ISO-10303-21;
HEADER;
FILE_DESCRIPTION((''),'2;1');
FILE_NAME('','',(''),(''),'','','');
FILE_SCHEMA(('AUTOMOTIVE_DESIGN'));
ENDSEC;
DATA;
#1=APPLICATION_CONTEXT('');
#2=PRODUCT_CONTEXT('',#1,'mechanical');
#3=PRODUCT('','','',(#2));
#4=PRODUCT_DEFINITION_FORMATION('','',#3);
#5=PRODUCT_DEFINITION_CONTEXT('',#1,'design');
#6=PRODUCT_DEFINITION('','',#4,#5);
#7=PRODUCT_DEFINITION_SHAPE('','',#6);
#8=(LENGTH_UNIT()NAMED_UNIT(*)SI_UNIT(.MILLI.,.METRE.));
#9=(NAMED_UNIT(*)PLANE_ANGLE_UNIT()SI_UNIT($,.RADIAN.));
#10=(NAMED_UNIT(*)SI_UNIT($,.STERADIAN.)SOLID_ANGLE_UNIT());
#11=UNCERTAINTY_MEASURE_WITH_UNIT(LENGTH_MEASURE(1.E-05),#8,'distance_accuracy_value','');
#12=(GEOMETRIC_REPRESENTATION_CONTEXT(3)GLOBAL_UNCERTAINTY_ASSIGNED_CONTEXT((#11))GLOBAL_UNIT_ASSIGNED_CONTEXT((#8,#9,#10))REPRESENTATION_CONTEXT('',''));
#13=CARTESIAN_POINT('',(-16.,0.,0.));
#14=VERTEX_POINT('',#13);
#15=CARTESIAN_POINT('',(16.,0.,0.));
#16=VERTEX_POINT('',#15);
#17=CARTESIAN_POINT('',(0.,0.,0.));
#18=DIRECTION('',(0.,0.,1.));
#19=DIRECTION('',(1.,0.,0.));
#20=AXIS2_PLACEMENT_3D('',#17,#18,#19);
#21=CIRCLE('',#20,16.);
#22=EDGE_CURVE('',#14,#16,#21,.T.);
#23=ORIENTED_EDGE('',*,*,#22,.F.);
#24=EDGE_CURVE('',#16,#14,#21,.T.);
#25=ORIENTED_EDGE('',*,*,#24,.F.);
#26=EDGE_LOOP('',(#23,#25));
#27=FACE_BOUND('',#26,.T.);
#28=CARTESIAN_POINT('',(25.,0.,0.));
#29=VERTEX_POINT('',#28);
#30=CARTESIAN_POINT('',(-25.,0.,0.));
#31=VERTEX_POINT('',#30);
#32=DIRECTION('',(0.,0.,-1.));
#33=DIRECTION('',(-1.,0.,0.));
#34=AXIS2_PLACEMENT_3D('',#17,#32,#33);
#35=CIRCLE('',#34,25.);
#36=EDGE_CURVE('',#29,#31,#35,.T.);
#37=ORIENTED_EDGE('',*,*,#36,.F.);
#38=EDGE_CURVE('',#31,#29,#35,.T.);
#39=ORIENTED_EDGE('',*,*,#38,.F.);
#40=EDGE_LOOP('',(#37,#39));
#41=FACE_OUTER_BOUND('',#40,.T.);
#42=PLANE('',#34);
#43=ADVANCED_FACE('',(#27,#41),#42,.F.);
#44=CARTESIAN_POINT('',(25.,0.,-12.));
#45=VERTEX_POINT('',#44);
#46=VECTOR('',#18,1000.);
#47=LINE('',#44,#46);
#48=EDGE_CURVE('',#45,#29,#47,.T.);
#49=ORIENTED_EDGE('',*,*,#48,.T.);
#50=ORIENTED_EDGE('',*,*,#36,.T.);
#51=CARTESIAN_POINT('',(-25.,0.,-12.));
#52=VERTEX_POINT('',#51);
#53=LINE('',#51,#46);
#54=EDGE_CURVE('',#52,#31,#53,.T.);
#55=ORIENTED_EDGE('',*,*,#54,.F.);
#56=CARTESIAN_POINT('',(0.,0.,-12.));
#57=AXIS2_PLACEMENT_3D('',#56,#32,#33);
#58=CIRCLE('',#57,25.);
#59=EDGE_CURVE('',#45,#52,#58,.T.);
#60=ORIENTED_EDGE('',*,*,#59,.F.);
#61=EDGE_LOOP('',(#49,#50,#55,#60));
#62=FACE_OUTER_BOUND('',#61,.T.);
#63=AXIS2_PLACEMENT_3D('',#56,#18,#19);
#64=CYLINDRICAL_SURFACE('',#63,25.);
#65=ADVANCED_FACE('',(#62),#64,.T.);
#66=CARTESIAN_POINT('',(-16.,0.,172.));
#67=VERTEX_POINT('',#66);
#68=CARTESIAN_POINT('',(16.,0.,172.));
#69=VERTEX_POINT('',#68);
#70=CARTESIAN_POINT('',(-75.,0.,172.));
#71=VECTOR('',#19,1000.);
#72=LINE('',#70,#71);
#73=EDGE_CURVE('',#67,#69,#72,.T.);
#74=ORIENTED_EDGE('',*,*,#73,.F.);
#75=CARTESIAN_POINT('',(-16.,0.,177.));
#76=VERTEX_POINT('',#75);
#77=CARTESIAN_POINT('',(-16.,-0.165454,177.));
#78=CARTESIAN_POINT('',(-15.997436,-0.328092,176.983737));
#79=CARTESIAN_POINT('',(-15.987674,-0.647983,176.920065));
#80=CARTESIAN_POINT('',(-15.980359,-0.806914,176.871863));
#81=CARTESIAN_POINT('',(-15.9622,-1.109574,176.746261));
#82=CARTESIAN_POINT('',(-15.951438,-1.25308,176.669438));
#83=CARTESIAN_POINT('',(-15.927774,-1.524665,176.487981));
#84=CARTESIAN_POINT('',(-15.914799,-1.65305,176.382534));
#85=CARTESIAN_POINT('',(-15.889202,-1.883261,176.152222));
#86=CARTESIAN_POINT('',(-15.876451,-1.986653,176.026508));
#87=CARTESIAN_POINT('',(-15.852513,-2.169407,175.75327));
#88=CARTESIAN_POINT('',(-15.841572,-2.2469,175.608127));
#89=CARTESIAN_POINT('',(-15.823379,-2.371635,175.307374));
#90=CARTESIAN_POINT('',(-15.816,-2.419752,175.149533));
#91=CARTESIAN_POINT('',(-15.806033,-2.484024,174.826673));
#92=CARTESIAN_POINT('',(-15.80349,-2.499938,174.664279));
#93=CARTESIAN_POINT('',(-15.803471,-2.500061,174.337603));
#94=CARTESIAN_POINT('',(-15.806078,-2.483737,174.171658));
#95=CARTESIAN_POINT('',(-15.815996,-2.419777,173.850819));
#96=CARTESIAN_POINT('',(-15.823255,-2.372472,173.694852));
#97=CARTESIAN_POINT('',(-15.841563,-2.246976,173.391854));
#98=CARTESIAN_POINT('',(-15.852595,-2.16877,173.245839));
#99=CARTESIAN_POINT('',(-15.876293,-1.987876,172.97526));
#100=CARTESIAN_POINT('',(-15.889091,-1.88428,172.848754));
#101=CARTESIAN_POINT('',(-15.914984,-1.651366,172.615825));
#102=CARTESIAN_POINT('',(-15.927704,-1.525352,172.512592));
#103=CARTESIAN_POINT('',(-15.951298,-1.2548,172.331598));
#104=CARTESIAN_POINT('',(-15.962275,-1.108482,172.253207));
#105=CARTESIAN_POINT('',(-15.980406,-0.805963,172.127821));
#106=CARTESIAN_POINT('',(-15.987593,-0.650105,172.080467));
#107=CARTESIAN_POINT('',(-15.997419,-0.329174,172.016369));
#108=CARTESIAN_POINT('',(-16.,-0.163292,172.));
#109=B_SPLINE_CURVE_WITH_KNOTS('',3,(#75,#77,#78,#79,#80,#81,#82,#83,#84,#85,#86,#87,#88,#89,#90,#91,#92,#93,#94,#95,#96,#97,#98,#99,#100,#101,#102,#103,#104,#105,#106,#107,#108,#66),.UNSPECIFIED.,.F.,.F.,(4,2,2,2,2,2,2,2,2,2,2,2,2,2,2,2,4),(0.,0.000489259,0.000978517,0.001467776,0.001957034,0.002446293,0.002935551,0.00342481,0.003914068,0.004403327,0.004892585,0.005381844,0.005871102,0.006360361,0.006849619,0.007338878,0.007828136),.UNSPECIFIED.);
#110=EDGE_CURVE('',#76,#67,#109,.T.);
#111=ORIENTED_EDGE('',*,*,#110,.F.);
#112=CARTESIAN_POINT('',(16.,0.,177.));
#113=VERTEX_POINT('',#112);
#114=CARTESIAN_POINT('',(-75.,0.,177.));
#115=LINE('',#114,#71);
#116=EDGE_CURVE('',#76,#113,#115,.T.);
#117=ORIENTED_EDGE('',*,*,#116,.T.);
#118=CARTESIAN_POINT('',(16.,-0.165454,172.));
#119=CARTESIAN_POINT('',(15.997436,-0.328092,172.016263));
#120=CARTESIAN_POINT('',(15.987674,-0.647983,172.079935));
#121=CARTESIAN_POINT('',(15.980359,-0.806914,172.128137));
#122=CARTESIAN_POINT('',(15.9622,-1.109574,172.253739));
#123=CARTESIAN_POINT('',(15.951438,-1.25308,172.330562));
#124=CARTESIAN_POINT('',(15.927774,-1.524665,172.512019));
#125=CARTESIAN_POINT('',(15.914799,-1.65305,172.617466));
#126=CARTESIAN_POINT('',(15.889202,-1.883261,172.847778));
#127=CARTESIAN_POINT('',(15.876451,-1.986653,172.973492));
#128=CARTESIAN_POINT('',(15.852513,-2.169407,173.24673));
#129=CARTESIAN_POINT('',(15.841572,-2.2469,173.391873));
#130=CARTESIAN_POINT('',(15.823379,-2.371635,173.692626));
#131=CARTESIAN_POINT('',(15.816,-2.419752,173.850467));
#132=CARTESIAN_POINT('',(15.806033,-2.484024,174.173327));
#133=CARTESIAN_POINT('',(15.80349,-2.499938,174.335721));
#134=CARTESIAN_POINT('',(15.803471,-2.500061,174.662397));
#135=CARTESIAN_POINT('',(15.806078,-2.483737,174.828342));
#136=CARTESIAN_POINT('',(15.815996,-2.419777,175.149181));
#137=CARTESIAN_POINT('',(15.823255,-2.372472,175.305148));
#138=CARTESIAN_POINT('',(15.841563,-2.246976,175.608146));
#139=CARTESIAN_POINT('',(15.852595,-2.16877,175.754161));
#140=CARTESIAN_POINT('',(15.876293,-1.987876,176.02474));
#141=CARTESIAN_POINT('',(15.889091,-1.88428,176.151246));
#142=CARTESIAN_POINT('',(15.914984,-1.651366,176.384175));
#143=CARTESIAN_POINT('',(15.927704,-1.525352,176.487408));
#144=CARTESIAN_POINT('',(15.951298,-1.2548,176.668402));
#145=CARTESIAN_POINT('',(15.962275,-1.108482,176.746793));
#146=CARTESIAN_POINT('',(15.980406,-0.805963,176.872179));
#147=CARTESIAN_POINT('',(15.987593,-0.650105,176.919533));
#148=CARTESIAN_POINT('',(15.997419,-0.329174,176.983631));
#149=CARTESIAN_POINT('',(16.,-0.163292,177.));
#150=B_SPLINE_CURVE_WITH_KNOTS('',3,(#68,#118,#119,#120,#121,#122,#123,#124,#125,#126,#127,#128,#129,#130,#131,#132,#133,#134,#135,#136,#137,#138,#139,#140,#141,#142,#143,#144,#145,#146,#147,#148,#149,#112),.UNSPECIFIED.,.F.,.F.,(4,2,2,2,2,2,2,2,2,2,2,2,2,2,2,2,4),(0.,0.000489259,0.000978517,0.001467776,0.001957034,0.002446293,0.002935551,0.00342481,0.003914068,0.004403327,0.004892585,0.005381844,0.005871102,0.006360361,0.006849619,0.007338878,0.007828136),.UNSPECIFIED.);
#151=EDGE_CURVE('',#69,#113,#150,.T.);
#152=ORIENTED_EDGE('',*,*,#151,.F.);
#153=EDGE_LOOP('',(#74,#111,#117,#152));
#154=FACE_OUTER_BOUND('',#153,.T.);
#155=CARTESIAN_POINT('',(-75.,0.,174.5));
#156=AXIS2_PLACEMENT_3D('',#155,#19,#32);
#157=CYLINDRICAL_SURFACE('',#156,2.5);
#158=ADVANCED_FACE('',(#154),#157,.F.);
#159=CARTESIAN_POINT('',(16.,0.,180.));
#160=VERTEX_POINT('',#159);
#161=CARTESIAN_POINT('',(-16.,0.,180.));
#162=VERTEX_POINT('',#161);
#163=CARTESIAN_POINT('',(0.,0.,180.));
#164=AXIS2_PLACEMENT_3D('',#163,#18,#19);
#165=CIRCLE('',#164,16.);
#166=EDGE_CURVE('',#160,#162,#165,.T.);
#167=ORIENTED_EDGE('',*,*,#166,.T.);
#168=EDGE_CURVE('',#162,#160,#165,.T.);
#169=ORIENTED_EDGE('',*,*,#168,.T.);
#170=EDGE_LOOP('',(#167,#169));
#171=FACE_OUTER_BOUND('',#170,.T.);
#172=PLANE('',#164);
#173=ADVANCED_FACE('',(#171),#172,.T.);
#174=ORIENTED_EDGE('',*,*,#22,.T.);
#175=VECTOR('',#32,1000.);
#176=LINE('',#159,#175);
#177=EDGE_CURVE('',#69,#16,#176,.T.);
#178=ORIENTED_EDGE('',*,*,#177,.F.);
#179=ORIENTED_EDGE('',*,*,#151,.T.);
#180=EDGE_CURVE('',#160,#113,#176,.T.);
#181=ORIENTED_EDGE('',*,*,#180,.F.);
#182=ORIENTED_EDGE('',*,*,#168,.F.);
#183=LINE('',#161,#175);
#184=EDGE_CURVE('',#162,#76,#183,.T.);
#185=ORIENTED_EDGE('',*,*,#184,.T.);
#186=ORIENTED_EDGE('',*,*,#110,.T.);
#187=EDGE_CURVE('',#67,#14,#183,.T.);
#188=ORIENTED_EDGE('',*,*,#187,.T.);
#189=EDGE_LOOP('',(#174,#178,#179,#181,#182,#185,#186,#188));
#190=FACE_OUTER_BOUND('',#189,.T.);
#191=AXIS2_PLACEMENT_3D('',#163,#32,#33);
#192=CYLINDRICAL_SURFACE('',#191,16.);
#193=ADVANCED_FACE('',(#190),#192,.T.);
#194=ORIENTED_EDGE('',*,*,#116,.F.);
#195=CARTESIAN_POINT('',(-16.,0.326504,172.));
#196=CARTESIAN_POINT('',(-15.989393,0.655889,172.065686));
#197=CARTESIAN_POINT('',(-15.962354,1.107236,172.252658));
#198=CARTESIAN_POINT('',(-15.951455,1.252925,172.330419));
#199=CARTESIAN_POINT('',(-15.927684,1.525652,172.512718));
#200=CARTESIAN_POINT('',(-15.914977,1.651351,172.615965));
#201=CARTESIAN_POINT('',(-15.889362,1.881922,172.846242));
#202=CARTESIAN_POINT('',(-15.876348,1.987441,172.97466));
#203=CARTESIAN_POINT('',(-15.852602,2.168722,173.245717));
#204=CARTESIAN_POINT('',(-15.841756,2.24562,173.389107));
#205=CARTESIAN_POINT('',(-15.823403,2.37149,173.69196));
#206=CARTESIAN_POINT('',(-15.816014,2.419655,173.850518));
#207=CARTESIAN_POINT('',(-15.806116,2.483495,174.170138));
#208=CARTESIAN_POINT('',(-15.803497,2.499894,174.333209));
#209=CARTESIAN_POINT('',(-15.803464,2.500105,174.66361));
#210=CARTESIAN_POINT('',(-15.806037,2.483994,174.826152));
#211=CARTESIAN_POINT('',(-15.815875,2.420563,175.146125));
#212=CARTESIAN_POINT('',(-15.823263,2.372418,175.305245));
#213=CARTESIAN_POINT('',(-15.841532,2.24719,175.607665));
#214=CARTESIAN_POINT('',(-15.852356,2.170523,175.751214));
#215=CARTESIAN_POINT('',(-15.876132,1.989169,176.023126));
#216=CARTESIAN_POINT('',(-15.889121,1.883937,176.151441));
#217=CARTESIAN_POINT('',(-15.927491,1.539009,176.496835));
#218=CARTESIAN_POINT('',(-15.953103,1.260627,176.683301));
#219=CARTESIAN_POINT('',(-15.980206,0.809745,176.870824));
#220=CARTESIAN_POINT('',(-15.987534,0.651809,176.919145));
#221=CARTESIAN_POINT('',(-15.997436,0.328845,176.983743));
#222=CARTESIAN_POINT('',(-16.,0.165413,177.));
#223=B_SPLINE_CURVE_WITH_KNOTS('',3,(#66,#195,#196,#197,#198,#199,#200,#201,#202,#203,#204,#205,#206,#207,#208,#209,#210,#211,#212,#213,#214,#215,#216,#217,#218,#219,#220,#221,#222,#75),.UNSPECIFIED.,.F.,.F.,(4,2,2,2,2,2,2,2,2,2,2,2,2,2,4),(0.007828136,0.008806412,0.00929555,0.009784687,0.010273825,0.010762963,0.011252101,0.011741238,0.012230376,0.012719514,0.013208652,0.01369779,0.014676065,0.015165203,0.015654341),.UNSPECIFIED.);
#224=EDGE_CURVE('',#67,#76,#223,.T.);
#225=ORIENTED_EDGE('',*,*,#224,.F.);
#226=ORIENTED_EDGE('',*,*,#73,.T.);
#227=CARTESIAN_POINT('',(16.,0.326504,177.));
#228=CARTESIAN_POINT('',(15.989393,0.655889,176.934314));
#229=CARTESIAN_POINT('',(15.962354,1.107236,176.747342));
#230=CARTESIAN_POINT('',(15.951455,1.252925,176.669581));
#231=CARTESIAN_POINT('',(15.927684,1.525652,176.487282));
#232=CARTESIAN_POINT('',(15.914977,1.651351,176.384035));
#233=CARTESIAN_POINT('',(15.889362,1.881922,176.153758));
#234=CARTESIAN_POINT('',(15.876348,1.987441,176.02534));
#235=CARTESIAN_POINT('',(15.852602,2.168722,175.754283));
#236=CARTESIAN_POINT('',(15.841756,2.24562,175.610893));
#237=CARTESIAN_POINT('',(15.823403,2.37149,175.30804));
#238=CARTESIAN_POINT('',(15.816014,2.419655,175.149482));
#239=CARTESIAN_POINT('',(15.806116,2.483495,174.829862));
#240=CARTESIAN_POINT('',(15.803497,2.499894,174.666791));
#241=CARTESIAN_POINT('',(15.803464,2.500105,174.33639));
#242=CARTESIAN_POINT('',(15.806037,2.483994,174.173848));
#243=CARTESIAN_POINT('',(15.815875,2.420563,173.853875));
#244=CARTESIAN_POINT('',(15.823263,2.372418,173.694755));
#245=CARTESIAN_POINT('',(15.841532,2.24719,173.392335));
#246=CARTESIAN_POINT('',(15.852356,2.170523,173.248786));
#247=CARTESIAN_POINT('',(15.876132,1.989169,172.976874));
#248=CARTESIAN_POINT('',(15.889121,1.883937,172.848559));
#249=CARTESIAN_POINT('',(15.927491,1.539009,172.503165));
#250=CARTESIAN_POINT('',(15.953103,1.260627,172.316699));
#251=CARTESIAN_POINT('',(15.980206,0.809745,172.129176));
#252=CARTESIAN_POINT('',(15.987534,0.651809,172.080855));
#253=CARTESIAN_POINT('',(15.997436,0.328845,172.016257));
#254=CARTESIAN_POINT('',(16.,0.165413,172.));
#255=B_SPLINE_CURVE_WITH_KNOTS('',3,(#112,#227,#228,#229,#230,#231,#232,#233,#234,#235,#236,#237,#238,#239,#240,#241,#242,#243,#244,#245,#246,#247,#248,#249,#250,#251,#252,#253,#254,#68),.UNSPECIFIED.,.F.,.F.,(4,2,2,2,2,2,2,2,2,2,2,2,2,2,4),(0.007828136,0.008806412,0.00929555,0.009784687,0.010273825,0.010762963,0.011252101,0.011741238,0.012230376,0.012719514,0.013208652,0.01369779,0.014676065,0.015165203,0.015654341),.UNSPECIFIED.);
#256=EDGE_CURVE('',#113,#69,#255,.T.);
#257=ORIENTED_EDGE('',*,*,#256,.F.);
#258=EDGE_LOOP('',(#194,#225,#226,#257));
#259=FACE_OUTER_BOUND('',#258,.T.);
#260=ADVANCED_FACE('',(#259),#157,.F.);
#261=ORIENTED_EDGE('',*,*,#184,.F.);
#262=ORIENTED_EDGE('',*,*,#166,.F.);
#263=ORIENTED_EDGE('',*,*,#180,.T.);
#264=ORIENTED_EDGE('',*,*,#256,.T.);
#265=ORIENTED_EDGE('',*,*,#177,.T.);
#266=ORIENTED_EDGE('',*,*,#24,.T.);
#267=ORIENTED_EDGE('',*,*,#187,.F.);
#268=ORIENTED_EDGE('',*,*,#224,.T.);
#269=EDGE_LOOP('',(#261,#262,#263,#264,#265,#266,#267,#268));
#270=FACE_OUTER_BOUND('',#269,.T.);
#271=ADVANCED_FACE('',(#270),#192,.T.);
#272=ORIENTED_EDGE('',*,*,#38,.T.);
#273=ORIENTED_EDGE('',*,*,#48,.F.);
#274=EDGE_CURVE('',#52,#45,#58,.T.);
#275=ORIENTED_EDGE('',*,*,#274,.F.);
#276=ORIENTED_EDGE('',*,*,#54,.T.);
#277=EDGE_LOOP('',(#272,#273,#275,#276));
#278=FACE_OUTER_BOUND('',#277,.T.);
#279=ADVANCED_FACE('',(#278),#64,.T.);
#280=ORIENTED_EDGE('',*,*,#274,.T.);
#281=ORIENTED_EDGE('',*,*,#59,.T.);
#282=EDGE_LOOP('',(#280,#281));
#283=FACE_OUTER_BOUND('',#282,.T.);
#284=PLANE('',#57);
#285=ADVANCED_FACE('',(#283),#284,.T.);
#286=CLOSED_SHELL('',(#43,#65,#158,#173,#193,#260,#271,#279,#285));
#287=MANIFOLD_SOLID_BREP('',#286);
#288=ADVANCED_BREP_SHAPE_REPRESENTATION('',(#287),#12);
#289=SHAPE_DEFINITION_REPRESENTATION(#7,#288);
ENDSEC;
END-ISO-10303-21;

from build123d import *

# Parameters (mm, degrees)
SHANK_PROFILE_32_R     = 16
SHANK_32X180_DEPTH     = 180
HEAD_PROFILE_50_R      = 25
HEAD_50X12_DEPTH       = 12
CROSS_HOLE_PROFILE_5_R = 2.5
CROSS_HOLE_5_DEPTH     = 75


with BuildPart() as part:
    # Shank Profile Ø32 → Shank Ø32x180 (new body)
    with BuildSketch(Plane.XY):
        with Locations(Location((0, 0, 0), (0, 0, 180))):
            Circle(SHANK_PROFILE_32_R)
    extrude(amount=SHANK_32X180_DEPTH)

    # Head Profile Ø50 → Head Ø50x12 (add)
    with BuildSketch(Plane(origin=(0, 0, 0), x_dir=(-1, 0, 0), z_dir=(0, 0, -1))):
        Circle(HEAD_PROFILE_50_R)
    extrude(amount=HEAD_50X12_DEPTH)

    # Cross Hole Profile Ø5 → Cross Hole Ø5 (cut, symmetric)
    with BuildSketch(Plane(origin=(0, 0, 0), x_dir=(0, 0, -1), z_dir=(1, 0, 0))):
        with Locations(Location((-174.5, 0, 0), (0, 0, 180))):
            Circle(CROSS_HOLE_PROFILE_5_R)
    extrude(amount=CROSS_HOLE_5_DEPTH, both=True, mode=Mode.SUBTRACT)


solid = part.part
